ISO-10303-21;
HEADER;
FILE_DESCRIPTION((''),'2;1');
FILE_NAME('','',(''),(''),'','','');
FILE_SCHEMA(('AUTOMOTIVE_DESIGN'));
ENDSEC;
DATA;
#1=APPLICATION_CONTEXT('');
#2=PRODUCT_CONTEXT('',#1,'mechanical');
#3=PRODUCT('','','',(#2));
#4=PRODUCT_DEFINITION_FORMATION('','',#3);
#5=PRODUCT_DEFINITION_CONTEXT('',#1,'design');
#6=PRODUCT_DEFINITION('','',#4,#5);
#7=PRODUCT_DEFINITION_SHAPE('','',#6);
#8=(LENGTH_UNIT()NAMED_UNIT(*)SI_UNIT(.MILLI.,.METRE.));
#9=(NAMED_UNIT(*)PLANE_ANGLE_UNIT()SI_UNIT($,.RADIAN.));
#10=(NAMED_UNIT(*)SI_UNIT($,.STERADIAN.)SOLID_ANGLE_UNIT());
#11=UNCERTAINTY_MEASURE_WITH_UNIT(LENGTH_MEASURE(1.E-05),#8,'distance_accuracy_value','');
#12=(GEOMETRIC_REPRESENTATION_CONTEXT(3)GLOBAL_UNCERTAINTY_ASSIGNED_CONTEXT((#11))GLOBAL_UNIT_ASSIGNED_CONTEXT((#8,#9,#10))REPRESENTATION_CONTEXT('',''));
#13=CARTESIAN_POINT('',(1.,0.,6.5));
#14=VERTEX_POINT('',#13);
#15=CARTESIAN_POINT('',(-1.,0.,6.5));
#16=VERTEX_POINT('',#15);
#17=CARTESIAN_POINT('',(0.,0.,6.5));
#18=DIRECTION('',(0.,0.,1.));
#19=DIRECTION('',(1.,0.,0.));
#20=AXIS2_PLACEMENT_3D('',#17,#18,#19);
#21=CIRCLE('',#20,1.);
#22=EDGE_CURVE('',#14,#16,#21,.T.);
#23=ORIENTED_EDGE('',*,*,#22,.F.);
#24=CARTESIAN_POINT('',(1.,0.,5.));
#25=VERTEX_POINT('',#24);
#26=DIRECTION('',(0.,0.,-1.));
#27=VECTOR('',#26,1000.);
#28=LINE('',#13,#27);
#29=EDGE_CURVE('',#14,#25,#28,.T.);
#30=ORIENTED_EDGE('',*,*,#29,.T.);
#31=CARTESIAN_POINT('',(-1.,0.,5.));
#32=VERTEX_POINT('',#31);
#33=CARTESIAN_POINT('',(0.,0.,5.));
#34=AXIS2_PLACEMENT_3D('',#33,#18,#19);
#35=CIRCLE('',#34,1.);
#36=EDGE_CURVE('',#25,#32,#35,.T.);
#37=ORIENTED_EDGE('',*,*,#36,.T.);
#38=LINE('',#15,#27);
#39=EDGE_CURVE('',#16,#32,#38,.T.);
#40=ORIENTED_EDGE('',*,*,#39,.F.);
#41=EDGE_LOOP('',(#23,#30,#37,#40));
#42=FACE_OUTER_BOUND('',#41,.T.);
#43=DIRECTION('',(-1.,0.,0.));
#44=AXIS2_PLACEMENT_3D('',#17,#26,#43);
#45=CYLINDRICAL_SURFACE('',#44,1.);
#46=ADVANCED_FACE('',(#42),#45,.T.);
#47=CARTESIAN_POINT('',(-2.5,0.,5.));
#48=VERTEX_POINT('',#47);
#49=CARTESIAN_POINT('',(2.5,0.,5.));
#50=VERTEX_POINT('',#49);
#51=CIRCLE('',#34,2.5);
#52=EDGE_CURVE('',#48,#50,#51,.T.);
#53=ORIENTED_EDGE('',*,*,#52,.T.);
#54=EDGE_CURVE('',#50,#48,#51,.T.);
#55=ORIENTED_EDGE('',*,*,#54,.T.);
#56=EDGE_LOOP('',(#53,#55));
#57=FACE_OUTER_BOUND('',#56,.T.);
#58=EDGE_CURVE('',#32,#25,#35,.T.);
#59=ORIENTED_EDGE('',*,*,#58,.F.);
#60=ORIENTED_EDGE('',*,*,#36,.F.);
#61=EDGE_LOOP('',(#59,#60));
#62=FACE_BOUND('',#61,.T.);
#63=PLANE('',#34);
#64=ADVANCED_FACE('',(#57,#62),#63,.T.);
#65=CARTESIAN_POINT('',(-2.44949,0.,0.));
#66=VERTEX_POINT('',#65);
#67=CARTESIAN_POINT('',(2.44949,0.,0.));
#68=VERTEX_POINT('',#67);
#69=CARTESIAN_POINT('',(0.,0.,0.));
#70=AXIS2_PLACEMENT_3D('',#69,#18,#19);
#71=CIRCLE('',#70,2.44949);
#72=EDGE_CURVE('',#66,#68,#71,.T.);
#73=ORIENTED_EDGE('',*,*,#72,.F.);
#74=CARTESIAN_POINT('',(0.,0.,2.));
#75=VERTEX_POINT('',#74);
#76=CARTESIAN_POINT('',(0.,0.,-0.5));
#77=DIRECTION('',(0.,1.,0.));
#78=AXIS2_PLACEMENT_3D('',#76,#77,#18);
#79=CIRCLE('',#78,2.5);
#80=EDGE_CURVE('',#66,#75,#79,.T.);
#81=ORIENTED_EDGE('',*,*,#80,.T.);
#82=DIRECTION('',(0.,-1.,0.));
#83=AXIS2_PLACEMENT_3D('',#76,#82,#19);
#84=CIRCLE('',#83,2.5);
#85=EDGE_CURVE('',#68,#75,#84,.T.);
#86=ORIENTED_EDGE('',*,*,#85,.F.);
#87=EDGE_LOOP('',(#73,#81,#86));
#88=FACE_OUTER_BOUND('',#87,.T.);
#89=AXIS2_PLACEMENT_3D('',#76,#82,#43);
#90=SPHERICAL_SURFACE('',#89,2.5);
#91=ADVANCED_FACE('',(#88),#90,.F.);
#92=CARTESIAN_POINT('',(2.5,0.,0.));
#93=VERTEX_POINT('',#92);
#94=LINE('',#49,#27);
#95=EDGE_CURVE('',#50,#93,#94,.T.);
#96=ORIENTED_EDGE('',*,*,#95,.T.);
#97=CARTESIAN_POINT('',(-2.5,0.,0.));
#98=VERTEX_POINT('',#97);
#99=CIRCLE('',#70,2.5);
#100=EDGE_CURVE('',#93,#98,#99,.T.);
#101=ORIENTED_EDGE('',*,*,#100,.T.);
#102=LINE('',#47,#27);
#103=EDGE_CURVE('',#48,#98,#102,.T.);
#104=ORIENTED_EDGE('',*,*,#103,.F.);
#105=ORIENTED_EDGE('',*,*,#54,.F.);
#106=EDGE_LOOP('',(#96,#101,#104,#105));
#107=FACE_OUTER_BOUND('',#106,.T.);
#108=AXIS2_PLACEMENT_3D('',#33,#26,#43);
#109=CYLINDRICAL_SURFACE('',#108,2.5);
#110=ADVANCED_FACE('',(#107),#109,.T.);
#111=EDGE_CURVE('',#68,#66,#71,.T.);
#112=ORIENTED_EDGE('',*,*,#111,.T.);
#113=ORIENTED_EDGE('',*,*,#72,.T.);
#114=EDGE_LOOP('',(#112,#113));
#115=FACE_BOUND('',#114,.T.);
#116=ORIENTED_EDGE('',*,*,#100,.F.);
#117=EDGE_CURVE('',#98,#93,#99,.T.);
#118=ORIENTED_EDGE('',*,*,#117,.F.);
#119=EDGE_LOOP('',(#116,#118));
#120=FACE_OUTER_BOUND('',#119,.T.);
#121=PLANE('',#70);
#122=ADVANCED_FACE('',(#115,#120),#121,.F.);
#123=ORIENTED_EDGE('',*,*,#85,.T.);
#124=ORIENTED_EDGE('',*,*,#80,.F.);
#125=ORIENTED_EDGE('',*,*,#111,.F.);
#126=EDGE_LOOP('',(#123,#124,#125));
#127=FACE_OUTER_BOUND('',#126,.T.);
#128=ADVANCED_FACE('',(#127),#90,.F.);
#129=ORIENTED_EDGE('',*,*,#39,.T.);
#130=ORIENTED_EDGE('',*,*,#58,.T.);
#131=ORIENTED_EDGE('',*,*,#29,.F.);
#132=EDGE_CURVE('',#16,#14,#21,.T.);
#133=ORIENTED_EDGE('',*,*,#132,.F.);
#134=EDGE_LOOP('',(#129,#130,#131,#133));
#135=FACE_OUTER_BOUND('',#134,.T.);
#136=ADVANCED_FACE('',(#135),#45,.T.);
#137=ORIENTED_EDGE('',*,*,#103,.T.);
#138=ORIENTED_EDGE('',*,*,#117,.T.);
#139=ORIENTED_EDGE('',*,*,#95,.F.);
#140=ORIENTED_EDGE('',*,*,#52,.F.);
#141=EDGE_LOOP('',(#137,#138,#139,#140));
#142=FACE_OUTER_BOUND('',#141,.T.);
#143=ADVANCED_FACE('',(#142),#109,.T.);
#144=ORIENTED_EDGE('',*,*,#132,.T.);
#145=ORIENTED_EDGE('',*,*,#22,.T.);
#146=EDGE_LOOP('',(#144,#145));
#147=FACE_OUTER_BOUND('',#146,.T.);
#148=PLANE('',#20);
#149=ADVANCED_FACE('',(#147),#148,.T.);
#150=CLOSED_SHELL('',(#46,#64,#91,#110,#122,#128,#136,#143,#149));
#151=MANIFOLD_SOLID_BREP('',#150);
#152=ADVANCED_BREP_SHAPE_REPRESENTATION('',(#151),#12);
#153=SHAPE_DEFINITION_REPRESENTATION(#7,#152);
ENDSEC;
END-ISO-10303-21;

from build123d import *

# Parameters (mm, degrees)
SKETCH1_R           = 2.5
BOSS_EXTRUDE1_DEPTH = 5
SKETCH2_R           = 1
BOSS_EXTRUDE2_DEPTH = 1.5


with BuildPart() as part:
    # Sketch1 → Boss-Extrude1 (new body)
    with BuildSketch(Plane.XY):
        Circle(SKETCH1_R)
    extrude(amount=BOSS_EXTRUDE1_DEPTH)

    # Sketch2 → Boss-Extrude2 (add)
    with BuildSketch(Plane.XY.offset(5)):
        Circle(SKETCH2_R)
    extrude(amount=BOSS_EXTRUDE2_DEPTH)

    # Sketch3 → Cut-Revolve1 (revolve, cut)
    with BuildSketch(Plane(origin=(0, 0, 0), x_dir=(1, 0, 0), z_dir=(0, 1, 0))):
        with BuildLine():
            Line((-2.449489743, 0), (0, 0))
            Line((0, 0), (0, -2))
            ThreePointArc((0, -2), (-1.58113883, -1.436491673), (-2.449489743, 0))
        make_face()
    revolve(axis=Axis((0, 0, 0), (0, 0, -1)), mode=Mode.SUBTRACT)


solid = part.part
